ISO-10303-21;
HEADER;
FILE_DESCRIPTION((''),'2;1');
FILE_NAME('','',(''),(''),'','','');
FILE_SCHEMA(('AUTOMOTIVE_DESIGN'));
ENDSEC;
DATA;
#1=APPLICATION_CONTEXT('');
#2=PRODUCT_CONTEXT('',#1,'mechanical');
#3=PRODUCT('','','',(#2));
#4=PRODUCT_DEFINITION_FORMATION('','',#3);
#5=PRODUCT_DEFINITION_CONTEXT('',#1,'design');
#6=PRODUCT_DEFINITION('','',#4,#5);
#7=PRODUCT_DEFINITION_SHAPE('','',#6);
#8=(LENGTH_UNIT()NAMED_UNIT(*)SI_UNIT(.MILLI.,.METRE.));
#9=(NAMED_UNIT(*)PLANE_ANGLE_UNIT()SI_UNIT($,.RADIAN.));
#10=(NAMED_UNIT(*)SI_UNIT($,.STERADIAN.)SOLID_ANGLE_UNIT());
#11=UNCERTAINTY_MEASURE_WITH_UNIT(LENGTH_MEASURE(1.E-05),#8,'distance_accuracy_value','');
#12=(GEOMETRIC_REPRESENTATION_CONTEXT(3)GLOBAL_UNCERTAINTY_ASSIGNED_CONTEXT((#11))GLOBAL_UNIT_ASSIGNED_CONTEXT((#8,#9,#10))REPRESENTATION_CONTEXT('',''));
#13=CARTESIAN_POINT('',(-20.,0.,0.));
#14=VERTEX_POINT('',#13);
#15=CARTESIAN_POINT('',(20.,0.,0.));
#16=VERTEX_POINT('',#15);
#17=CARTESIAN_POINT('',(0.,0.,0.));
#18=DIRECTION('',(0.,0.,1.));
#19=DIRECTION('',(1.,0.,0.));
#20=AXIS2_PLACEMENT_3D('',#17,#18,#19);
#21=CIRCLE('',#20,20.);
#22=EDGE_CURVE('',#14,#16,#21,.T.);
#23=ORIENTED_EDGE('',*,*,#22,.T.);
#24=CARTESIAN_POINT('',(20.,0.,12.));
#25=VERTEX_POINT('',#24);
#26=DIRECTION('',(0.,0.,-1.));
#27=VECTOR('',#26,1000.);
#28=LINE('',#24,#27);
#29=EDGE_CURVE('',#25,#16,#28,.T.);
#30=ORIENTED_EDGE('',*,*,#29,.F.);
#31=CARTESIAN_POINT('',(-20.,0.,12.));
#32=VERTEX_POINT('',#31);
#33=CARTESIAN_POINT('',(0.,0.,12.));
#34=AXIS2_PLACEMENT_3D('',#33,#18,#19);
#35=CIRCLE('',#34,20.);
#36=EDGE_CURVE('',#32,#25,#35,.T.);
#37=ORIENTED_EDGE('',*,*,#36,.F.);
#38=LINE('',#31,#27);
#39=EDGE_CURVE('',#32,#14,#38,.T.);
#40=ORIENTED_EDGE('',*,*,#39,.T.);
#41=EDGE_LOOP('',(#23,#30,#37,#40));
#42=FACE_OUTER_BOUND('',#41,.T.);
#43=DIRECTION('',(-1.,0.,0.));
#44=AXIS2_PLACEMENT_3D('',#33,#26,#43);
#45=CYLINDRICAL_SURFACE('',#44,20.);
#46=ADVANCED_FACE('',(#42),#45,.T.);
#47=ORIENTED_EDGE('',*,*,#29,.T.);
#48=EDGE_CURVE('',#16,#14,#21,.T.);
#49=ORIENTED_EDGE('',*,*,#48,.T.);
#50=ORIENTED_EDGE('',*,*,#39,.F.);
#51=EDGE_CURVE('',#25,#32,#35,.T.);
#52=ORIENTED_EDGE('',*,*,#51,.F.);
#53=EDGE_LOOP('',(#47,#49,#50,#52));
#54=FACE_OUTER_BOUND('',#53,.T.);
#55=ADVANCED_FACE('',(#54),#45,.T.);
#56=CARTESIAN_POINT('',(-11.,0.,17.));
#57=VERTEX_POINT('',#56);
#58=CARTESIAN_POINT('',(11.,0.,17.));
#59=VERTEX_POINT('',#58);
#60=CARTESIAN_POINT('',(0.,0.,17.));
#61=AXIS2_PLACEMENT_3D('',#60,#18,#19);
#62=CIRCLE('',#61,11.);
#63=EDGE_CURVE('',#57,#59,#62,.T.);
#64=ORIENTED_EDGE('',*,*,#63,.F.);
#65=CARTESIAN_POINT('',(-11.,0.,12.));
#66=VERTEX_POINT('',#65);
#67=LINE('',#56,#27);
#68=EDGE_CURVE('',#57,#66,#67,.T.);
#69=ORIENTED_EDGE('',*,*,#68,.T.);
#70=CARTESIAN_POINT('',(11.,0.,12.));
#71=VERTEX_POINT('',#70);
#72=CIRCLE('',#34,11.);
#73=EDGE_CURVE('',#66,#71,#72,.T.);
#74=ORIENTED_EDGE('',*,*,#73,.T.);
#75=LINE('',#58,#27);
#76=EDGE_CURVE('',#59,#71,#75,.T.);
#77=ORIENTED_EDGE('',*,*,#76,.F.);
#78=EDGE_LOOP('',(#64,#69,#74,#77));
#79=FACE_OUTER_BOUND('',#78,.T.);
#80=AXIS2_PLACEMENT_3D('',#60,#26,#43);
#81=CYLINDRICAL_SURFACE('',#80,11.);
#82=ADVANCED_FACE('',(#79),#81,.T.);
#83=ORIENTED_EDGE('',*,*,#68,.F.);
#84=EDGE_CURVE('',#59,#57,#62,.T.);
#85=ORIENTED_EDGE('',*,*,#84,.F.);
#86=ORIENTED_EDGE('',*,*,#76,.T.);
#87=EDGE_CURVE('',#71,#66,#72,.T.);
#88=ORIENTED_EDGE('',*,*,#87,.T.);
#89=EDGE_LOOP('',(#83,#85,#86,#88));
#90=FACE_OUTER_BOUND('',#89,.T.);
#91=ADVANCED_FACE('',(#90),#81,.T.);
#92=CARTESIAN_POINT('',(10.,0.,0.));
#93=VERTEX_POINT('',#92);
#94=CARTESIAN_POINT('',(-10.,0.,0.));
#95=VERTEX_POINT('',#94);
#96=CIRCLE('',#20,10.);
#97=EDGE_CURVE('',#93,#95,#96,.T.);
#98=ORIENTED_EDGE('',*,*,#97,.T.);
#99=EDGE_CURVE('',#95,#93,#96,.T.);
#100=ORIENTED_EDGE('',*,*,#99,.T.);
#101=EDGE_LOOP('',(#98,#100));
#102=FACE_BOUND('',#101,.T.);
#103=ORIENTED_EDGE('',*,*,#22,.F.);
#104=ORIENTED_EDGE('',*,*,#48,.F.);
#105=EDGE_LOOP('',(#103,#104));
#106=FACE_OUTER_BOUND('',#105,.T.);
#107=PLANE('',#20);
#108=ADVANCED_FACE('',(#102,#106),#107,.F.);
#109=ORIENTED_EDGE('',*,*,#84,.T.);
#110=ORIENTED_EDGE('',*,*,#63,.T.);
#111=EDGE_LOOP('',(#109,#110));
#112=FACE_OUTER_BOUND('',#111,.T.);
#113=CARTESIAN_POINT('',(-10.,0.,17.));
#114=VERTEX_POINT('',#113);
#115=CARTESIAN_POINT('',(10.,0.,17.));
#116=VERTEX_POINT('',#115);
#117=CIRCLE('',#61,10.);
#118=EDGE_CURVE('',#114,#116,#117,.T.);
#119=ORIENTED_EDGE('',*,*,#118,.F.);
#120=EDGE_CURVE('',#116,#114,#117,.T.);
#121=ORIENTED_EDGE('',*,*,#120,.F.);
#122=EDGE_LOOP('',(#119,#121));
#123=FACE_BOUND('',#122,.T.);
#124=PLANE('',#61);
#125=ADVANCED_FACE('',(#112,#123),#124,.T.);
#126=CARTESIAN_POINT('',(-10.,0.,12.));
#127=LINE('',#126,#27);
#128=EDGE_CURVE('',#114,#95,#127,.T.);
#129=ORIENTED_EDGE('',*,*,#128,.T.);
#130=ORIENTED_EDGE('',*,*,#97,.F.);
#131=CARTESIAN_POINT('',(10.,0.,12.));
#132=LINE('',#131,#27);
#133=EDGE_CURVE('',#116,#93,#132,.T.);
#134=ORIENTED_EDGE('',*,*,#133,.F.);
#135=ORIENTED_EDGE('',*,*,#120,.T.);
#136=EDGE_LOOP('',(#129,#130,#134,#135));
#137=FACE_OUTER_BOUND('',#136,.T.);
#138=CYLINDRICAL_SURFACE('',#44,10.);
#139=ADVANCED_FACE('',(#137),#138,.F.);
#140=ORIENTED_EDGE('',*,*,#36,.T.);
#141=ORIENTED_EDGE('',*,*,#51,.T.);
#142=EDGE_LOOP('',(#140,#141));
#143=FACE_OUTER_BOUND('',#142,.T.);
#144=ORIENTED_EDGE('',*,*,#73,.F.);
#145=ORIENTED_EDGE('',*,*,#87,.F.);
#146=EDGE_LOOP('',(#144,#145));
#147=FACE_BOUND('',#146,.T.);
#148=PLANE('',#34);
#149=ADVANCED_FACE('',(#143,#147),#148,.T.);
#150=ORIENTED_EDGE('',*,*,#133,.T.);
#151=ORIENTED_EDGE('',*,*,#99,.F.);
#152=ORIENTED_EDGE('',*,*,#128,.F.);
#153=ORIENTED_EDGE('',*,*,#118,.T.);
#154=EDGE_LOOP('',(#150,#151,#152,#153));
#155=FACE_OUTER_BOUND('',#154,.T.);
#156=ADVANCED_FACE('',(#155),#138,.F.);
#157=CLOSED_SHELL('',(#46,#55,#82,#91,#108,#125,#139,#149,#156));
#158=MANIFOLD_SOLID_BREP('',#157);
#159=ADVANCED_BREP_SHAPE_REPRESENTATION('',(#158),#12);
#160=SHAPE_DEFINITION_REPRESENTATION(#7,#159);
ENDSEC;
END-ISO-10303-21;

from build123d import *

# Parameters (mm, degrees)
SKETCH1_R           = 20
SKETCH1_R_2         = 10
BOSS_EXTRUDE1_DEPTH = 12
SKETCH2_R           = 11
SKETCH2_R_2         = 10
BOSS_EXTRUDE2_DEPTH = 5


with BuildPart() as part:
    # Sketch1 → Boss-Extrude1 (new body)
    with BuildSketch(Plane.XY):
        Circle(SKETCH1_R)
        Circle(SKETCH1_R_2, mode=Mode.SUBTRACT)
    extrude(amount=BOSS_EXTRUDE1_DEPTH)

    # Sketch2 → Boss-Extrude2 (add)
    with BuildSketch(Plane.XY.offset(12)):
        Circle(SKETCH2_R)
        Circle(SKETCH2_R_2, mode=Mode.SUBTRACT)
    extrude(amount=BOSS_EXTRUDE2_DEPTH)


solid = part.part
